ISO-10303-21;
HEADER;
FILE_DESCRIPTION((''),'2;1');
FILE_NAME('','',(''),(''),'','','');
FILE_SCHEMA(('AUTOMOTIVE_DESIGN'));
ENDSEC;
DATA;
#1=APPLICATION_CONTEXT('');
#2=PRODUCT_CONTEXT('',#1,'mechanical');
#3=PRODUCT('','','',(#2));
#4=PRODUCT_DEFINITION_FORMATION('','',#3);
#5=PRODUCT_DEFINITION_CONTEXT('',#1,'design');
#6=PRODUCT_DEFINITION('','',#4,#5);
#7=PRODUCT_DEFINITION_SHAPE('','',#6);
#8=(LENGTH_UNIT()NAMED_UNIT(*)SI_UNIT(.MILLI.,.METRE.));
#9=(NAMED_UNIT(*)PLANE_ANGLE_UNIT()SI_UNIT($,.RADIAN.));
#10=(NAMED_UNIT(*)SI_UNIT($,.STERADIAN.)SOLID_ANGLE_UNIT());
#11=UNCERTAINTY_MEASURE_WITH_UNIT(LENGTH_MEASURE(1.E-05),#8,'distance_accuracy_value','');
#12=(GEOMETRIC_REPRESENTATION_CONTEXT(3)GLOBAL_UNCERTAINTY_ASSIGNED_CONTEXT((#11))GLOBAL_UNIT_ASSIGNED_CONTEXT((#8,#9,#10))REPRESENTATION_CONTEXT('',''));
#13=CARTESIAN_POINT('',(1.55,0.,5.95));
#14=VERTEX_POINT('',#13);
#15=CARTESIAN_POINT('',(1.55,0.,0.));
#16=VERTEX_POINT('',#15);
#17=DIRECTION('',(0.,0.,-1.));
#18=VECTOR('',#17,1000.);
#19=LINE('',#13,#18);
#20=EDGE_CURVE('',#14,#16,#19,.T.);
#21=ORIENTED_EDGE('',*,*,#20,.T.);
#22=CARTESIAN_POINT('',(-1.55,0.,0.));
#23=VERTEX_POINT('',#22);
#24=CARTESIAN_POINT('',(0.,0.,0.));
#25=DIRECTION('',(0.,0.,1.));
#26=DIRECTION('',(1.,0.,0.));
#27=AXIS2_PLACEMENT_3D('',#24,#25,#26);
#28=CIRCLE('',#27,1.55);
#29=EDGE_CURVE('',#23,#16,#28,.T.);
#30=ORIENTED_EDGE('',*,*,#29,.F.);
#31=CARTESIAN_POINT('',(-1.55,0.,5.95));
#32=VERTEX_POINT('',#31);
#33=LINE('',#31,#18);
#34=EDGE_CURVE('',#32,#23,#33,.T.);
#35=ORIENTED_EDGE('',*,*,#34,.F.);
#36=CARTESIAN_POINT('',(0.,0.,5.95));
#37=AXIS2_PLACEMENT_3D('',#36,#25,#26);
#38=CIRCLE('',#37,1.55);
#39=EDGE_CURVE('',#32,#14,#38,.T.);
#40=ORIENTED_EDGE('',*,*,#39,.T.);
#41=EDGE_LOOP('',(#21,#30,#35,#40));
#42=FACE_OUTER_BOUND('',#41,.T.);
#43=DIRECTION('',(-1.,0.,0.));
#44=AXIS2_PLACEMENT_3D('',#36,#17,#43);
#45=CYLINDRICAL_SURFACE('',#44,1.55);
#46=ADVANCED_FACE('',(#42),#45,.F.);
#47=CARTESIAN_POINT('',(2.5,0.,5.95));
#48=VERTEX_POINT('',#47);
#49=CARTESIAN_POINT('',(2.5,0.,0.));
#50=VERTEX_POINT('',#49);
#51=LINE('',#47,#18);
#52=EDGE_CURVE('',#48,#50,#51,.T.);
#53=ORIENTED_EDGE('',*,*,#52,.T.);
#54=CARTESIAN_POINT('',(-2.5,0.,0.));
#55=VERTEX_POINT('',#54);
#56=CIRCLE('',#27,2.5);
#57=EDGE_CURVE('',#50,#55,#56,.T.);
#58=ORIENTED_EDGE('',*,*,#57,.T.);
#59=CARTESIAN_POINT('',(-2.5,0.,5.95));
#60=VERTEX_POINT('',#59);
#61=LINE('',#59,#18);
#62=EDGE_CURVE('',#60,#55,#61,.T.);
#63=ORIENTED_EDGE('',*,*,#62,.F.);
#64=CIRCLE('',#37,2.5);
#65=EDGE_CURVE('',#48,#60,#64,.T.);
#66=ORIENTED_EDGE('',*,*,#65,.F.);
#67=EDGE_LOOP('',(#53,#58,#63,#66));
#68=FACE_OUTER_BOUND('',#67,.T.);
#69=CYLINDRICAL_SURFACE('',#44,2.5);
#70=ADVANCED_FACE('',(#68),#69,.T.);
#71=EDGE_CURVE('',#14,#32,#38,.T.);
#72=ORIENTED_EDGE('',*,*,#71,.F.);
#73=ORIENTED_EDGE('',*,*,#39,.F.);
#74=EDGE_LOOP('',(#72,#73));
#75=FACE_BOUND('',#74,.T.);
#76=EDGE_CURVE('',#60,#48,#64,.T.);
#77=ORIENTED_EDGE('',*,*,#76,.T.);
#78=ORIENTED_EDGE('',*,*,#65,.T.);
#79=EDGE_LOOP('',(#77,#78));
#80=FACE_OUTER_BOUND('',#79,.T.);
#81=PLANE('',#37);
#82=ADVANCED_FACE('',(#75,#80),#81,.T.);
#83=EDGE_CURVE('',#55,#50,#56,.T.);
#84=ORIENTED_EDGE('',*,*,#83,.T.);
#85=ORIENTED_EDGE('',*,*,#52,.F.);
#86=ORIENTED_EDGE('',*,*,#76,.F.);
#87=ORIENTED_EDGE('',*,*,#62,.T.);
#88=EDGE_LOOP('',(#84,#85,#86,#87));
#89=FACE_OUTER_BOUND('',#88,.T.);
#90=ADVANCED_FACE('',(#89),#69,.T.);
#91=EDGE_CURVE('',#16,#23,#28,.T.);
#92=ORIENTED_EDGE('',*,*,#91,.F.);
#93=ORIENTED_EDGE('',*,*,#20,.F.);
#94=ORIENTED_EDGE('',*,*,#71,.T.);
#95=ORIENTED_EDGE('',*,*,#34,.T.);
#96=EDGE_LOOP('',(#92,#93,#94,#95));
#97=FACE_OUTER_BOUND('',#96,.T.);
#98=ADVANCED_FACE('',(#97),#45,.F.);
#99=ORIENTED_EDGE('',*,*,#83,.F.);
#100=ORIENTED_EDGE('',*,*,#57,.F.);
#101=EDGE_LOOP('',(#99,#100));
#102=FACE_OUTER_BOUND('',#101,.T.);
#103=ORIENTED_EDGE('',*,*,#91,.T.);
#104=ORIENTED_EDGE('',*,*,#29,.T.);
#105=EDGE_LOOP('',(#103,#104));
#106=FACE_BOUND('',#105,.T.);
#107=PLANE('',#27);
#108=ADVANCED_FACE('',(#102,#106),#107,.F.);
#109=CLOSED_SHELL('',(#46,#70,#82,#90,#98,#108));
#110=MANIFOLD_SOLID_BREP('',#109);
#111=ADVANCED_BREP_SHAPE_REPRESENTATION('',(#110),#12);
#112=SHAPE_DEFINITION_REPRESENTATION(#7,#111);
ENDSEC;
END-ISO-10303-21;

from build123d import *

# Parameters (mm, degrees)
SKETCH_1_R      = 2.5
SKETCH_1_R_2    = 1.55
EXTRUDE_1_DEPTH = 5.95


with BuildPart() as part:
    # 草图1 → 凸台-拉伸1 (new body)
    with BuildSketch(Plane.XY):
        Circle(SKETCH_1_R)
        Circle(SKETCH_1_R_2, mode=Mode.SUBTRACT)
    extrude(amount=EXTRUDE_1_DEPTH)


solid = part.part
